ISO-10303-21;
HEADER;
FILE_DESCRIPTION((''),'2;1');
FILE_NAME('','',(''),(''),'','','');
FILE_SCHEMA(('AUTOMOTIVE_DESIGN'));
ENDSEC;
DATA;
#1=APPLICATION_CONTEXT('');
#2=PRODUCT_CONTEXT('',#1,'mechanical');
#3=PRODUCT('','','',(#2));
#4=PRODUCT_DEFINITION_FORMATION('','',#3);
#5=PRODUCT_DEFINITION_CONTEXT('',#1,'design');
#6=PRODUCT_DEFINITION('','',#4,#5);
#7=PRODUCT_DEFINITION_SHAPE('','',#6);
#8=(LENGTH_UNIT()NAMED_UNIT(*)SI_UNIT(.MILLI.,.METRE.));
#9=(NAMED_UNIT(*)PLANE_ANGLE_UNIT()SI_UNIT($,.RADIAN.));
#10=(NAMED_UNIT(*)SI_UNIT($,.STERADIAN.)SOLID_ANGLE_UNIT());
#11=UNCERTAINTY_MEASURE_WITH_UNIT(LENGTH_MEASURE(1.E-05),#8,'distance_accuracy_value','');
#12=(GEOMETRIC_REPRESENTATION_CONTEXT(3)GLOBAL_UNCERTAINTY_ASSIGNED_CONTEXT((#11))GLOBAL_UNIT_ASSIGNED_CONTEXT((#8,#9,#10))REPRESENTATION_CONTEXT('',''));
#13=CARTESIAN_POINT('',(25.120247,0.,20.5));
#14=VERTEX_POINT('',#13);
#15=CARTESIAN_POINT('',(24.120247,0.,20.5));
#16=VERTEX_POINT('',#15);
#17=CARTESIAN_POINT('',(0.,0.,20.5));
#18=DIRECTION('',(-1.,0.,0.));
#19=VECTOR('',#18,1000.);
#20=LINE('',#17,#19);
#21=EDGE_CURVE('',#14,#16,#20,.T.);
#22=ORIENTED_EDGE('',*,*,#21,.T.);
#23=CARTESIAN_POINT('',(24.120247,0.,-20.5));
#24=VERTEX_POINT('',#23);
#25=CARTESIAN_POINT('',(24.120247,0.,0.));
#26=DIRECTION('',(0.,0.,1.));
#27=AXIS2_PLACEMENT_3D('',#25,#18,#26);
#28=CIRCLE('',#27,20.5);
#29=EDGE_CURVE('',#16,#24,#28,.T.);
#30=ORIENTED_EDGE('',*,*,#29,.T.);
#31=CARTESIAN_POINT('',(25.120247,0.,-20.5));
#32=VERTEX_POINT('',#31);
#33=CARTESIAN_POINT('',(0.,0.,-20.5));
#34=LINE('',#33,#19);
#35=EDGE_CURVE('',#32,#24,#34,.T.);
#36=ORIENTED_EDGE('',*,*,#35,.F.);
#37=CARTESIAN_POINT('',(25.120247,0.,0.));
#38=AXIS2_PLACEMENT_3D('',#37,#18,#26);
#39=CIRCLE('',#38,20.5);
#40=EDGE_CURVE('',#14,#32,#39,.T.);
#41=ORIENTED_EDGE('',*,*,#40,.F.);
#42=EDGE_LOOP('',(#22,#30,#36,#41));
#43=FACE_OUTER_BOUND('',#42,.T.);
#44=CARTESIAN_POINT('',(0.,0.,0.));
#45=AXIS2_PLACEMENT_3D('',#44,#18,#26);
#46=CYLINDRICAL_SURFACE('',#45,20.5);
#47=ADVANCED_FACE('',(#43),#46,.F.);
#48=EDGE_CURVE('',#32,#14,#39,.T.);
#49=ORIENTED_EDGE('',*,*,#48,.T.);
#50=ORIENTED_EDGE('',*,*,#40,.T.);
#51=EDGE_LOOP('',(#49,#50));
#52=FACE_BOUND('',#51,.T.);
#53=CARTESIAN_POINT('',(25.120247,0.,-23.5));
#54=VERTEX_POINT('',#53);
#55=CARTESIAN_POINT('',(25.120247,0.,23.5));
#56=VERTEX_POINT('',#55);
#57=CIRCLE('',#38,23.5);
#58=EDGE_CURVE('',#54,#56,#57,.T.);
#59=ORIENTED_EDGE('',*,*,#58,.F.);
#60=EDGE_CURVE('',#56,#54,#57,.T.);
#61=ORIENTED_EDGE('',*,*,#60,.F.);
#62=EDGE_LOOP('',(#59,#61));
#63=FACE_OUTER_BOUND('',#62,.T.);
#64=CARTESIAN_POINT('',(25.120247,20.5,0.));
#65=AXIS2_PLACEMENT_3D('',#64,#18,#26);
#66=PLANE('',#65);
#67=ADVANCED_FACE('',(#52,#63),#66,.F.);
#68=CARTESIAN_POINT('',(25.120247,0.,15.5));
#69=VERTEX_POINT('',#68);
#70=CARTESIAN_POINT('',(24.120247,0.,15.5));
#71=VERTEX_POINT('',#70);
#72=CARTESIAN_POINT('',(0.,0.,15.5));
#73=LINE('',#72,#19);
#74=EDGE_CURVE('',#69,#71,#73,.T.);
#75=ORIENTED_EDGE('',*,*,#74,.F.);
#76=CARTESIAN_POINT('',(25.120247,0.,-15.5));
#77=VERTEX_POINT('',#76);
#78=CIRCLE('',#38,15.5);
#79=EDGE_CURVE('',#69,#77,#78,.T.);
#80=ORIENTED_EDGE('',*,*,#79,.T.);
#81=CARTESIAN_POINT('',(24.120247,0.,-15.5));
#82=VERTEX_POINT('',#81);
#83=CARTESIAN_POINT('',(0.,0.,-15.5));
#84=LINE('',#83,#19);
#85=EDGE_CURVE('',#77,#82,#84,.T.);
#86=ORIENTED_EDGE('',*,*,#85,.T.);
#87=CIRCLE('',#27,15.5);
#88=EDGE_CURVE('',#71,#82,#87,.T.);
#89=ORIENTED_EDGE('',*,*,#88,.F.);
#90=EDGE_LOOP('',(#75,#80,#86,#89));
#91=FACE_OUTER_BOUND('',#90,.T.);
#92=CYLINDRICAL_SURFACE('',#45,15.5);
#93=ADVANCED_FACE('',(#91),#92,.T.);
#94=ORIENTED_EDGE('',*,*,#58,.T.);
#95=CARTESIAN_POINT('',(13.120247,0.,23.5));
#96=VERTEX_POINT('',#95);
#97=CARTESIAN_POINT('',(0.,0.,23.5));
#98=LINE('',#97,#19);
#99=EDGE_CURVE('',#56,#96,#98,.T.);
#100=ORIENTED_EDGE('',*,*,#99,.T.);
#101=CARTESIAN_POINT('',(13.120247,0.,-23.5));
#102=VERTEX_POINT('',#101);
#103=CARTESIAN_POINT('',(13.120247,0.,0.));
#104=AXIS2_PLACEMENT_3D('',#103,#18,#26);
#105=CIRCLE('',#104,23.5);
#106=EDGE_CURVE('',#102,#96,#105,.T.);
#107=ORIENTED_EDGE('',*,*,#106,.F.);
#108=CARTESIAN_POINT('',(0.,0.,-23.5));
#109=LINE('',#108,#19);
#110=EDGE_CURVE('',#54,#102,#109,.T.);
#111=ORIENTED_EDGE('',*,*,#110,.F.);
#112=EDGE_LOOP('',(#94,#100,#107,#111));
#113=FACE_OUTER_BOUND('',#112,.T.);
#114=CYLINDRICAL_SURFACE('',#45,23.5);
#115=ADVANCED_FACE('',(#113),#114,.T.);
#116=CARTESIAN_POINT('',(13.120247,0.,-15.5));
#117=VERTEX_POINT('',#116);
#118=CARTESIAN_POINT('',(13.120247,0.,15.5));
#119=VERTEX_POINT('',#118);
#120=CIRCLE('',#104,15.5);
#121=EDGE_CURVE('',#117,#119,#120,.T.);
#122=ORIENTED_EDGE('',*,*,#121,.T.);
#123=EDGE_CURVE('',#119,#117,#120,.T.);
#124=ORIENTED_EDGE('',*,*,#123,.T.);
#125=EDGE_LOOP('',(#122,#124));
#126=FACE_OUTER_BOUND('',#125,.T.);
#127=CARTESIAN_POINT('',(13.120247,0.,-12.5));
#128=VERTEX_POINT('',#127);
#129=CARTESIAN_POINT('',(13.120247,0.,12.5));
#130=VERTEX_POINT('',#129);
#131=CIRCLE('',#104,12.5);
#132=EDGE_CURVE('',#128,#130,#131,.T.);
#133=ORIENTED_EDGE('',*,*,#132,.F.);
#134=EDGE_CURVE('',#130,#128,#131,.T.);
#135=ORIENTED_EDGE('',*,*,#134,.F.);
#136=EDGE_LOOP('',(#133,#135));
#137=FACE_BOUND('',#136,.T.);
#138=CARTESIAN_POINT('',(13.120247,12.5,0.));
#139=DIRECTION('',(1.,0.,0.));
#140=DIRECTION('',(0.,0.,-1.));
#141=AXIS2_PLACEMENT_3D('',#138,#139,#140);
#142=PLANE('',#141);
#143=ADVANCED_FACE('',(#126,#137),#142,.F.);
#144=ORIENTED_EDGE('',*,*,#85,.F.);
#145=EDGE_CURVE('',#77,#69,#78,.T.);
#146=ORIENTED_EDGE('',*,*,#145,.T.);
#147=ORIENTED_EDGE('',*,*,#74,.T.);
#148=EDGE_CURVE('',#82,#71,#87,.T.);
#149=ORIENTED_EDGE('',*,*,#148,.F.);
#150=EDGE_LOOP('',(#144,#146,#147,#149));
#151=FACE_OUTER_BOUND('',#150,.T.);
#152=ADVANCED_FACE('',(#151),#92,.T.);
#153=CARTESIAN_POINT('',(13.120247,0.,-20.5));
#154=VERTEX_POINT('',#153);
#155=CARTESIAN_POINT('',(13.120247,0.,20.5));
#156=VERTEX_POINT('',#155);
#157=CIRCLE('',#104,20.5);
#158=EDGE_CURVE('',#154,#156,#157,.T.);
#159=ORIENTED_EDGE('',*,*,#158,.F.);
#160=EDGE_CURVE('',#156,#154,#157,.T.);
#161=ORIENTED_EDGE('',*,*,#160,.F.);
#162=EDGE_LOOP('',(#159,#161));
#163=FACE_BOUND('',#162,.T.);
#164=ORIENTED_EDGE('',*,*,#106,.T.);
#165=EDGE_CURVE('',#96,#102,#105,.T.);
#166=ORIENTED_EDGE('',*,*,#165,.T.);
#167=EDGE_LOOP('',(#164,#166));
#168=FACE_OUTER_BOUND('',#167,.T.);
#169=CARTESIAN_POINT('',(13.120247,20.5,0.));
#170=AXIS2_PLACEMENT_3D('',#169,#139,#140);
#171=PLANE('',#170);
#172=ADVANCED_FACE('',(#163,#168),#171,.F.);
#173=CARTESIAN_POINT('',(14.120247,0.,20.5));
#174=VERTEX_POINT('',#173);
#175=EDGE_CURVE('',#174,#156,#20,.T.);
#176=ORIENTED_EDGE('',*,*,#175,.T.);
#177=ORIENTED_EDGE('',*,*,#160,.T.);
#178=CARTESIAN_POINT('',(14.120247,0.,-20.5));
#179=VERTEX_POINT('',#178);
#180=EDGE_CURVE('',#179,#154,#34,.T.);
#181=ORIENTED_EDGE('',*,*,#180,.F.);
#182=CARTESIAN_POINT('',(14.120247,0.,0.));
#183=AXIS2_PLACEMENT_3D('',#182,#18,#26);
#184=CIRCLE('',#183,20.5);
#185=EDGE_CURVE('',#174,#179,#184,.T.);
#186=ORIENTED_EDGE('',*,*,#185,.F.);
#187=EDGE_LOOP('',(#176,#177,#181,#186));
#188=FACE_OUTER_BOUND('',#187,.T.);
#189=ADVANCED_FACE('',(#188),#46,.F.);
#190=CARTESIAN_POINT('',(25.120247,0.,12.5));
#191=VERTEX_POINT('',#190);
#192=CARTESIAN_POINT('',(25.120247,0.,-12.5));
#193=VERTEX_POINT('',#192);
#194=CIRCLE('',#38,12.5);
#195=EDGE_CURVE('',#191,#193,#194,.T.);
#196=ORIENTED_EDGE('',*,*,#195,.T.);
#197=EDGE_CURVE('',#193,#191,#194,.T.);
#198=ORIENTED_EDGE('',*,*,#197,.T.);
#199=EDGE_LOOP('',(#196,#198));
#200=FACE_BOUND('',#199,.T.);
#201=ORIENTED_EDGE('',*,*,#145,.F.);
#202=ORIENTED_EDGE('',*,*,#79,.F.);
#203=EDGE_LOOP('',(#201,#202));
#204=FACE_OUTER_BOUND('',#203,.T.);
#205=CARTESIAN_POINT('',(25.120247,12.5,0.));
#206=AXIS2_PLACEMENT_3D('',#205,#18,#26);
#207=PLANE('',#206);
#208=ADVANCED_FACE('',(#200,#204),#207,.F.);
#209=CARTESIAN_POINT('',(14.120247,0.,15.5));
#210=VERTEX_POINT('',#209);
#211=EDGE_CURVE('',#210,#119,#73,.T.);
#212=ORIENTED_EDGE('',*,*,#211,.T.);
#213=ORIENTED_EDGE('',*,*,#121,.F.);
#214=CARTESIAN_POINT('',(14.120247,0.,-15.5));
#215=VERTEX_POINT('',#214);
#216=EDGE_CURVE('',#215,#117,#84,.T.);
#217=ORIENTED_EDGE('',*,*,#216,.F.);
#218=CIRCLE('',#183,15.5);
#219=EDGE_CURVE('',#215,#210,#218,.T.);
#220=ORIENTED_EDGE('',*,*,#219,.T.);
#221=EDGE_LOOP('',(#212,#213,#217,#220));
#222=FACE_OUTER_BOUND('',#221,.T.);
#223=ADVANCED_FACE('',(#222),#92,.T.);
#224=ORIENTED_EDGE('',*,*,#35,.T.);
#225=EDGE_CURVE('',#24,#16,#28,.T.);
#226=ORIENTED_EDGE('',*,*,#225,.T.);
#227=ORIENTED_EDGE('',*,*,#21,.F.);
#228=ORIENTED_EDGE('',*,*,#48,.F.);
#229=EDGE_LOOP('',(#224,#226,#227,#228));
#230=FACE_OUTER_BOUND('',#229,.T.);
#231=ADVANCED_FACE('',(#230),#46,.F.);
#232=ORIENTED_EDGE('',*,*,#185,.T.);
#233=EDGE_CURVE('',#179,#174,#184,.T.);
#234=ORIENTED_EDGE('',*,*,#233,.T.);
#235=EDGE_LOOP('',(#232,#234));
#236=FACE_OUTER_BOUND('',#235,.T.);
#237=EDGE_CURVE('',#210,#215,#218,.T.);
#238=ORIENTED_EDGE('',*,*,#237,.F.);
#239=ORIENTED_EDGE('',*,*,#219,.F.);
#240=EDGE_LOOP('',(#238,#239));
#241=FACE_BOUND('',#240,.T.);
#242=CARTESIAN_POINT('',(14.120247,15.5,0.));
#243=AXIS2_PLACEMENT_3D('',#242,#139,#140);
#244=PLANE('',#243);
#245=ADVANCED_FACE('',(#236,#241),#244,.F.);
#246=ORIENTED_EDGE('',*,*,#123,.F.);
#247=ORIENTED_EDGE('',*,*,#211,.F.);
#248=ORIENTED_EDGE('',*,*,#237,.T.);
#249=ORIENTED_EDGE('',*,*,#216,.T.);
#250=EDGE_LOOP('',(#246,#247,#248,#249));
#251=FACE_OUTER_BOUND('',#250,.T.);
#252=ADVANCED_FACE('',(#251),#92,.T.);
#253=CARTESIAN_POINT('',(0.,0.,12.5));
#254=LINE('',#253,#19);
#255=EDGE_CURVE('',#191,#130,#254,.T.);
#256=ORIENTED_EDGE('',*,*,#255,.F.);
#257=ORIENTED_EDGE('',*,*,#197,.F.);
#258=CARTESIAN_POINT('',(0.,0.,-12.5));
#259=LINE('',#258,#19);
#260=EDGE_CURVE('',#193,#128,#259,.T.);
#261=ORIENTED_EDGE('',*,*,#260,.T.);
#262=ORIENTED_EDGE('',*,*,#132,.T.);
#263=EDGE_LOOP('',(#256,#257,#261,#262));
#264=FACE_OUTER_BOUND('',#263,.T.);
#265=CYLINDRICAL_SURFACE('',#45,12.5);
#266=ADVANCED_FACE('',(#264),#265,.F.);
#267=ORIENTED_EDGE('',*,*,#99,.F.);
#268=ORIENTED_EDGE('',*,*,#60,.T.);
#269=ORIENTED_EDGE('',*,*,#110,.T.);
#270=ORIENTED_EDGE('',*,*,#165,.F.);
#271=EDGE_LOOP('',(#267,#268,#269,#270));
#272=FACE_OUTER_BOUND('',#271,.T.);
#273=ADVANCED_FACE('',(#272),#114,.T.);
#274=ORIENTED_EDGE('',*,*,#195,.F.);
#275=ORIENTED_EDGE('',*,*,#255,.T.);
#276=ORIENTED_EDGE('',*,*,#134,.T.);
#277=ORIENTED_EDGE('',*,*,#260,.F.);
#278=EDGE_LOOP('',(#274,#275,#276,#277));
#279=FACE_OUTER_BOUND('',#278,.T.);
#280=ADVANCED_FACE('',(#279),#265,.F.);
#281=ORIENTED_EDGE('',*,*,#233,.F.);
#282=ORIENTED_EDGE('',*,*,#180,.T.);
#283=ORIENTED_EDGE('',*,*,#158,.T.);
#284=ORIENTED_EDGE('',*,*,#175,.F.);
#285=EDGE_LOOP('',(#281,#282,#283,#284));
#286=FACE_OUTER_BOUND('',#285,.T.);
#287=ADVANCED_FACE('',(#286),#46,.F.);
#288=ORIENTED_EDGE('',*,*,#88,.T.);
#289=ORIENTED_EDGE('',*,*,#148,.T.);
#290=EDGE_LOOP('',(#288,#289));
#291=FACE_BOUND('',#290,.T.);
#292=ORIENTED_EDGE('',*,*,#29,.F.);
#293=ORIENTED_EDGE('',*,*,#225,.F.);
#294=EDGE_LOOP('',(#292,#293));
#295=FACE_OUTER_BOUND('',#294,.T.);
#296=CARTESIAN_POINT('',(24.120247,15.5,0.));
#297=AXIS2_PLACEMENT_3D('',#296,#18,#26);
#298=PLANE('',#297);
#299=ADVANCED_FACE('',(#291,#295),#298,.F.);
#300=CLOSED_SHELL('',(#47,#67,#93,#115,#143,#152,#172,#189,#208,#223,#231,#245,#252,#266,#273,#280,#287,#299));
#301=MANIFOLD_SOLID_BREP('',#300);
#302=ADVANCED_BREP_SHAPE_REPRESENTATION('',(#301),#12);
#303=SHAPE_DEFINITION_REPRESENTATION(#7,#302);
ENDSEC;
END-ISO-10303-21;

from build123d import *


with BuildPart() as part:
    # Sketch1 → Revolve1 (revolve)
    with BuildSketch(Plane.XY, mode=Mode.PRIVATE) as revolve1_sk:
        Polygon((13.120246846, 20.5), (13.120246846, 23.5), (25.120246846, 23.5), (25.120246846, 20.5), (24.120246846, 20.5), (24.120246846, 15.5), (25.120246846, 15.5), (25.120246846, 12.5), (13.120246846, 12.5), (13.120246846, 15.5), (14.120246846, 15.5), (14.120246846, 20.5), align=None)
    revolve(revolve1_sk.sketch.rotate(Axis((0, 0, 0), (1, 0, 0)), 90), axis=Axis((0, 0, 0), (1, 0, 0)))


solid = part.part
